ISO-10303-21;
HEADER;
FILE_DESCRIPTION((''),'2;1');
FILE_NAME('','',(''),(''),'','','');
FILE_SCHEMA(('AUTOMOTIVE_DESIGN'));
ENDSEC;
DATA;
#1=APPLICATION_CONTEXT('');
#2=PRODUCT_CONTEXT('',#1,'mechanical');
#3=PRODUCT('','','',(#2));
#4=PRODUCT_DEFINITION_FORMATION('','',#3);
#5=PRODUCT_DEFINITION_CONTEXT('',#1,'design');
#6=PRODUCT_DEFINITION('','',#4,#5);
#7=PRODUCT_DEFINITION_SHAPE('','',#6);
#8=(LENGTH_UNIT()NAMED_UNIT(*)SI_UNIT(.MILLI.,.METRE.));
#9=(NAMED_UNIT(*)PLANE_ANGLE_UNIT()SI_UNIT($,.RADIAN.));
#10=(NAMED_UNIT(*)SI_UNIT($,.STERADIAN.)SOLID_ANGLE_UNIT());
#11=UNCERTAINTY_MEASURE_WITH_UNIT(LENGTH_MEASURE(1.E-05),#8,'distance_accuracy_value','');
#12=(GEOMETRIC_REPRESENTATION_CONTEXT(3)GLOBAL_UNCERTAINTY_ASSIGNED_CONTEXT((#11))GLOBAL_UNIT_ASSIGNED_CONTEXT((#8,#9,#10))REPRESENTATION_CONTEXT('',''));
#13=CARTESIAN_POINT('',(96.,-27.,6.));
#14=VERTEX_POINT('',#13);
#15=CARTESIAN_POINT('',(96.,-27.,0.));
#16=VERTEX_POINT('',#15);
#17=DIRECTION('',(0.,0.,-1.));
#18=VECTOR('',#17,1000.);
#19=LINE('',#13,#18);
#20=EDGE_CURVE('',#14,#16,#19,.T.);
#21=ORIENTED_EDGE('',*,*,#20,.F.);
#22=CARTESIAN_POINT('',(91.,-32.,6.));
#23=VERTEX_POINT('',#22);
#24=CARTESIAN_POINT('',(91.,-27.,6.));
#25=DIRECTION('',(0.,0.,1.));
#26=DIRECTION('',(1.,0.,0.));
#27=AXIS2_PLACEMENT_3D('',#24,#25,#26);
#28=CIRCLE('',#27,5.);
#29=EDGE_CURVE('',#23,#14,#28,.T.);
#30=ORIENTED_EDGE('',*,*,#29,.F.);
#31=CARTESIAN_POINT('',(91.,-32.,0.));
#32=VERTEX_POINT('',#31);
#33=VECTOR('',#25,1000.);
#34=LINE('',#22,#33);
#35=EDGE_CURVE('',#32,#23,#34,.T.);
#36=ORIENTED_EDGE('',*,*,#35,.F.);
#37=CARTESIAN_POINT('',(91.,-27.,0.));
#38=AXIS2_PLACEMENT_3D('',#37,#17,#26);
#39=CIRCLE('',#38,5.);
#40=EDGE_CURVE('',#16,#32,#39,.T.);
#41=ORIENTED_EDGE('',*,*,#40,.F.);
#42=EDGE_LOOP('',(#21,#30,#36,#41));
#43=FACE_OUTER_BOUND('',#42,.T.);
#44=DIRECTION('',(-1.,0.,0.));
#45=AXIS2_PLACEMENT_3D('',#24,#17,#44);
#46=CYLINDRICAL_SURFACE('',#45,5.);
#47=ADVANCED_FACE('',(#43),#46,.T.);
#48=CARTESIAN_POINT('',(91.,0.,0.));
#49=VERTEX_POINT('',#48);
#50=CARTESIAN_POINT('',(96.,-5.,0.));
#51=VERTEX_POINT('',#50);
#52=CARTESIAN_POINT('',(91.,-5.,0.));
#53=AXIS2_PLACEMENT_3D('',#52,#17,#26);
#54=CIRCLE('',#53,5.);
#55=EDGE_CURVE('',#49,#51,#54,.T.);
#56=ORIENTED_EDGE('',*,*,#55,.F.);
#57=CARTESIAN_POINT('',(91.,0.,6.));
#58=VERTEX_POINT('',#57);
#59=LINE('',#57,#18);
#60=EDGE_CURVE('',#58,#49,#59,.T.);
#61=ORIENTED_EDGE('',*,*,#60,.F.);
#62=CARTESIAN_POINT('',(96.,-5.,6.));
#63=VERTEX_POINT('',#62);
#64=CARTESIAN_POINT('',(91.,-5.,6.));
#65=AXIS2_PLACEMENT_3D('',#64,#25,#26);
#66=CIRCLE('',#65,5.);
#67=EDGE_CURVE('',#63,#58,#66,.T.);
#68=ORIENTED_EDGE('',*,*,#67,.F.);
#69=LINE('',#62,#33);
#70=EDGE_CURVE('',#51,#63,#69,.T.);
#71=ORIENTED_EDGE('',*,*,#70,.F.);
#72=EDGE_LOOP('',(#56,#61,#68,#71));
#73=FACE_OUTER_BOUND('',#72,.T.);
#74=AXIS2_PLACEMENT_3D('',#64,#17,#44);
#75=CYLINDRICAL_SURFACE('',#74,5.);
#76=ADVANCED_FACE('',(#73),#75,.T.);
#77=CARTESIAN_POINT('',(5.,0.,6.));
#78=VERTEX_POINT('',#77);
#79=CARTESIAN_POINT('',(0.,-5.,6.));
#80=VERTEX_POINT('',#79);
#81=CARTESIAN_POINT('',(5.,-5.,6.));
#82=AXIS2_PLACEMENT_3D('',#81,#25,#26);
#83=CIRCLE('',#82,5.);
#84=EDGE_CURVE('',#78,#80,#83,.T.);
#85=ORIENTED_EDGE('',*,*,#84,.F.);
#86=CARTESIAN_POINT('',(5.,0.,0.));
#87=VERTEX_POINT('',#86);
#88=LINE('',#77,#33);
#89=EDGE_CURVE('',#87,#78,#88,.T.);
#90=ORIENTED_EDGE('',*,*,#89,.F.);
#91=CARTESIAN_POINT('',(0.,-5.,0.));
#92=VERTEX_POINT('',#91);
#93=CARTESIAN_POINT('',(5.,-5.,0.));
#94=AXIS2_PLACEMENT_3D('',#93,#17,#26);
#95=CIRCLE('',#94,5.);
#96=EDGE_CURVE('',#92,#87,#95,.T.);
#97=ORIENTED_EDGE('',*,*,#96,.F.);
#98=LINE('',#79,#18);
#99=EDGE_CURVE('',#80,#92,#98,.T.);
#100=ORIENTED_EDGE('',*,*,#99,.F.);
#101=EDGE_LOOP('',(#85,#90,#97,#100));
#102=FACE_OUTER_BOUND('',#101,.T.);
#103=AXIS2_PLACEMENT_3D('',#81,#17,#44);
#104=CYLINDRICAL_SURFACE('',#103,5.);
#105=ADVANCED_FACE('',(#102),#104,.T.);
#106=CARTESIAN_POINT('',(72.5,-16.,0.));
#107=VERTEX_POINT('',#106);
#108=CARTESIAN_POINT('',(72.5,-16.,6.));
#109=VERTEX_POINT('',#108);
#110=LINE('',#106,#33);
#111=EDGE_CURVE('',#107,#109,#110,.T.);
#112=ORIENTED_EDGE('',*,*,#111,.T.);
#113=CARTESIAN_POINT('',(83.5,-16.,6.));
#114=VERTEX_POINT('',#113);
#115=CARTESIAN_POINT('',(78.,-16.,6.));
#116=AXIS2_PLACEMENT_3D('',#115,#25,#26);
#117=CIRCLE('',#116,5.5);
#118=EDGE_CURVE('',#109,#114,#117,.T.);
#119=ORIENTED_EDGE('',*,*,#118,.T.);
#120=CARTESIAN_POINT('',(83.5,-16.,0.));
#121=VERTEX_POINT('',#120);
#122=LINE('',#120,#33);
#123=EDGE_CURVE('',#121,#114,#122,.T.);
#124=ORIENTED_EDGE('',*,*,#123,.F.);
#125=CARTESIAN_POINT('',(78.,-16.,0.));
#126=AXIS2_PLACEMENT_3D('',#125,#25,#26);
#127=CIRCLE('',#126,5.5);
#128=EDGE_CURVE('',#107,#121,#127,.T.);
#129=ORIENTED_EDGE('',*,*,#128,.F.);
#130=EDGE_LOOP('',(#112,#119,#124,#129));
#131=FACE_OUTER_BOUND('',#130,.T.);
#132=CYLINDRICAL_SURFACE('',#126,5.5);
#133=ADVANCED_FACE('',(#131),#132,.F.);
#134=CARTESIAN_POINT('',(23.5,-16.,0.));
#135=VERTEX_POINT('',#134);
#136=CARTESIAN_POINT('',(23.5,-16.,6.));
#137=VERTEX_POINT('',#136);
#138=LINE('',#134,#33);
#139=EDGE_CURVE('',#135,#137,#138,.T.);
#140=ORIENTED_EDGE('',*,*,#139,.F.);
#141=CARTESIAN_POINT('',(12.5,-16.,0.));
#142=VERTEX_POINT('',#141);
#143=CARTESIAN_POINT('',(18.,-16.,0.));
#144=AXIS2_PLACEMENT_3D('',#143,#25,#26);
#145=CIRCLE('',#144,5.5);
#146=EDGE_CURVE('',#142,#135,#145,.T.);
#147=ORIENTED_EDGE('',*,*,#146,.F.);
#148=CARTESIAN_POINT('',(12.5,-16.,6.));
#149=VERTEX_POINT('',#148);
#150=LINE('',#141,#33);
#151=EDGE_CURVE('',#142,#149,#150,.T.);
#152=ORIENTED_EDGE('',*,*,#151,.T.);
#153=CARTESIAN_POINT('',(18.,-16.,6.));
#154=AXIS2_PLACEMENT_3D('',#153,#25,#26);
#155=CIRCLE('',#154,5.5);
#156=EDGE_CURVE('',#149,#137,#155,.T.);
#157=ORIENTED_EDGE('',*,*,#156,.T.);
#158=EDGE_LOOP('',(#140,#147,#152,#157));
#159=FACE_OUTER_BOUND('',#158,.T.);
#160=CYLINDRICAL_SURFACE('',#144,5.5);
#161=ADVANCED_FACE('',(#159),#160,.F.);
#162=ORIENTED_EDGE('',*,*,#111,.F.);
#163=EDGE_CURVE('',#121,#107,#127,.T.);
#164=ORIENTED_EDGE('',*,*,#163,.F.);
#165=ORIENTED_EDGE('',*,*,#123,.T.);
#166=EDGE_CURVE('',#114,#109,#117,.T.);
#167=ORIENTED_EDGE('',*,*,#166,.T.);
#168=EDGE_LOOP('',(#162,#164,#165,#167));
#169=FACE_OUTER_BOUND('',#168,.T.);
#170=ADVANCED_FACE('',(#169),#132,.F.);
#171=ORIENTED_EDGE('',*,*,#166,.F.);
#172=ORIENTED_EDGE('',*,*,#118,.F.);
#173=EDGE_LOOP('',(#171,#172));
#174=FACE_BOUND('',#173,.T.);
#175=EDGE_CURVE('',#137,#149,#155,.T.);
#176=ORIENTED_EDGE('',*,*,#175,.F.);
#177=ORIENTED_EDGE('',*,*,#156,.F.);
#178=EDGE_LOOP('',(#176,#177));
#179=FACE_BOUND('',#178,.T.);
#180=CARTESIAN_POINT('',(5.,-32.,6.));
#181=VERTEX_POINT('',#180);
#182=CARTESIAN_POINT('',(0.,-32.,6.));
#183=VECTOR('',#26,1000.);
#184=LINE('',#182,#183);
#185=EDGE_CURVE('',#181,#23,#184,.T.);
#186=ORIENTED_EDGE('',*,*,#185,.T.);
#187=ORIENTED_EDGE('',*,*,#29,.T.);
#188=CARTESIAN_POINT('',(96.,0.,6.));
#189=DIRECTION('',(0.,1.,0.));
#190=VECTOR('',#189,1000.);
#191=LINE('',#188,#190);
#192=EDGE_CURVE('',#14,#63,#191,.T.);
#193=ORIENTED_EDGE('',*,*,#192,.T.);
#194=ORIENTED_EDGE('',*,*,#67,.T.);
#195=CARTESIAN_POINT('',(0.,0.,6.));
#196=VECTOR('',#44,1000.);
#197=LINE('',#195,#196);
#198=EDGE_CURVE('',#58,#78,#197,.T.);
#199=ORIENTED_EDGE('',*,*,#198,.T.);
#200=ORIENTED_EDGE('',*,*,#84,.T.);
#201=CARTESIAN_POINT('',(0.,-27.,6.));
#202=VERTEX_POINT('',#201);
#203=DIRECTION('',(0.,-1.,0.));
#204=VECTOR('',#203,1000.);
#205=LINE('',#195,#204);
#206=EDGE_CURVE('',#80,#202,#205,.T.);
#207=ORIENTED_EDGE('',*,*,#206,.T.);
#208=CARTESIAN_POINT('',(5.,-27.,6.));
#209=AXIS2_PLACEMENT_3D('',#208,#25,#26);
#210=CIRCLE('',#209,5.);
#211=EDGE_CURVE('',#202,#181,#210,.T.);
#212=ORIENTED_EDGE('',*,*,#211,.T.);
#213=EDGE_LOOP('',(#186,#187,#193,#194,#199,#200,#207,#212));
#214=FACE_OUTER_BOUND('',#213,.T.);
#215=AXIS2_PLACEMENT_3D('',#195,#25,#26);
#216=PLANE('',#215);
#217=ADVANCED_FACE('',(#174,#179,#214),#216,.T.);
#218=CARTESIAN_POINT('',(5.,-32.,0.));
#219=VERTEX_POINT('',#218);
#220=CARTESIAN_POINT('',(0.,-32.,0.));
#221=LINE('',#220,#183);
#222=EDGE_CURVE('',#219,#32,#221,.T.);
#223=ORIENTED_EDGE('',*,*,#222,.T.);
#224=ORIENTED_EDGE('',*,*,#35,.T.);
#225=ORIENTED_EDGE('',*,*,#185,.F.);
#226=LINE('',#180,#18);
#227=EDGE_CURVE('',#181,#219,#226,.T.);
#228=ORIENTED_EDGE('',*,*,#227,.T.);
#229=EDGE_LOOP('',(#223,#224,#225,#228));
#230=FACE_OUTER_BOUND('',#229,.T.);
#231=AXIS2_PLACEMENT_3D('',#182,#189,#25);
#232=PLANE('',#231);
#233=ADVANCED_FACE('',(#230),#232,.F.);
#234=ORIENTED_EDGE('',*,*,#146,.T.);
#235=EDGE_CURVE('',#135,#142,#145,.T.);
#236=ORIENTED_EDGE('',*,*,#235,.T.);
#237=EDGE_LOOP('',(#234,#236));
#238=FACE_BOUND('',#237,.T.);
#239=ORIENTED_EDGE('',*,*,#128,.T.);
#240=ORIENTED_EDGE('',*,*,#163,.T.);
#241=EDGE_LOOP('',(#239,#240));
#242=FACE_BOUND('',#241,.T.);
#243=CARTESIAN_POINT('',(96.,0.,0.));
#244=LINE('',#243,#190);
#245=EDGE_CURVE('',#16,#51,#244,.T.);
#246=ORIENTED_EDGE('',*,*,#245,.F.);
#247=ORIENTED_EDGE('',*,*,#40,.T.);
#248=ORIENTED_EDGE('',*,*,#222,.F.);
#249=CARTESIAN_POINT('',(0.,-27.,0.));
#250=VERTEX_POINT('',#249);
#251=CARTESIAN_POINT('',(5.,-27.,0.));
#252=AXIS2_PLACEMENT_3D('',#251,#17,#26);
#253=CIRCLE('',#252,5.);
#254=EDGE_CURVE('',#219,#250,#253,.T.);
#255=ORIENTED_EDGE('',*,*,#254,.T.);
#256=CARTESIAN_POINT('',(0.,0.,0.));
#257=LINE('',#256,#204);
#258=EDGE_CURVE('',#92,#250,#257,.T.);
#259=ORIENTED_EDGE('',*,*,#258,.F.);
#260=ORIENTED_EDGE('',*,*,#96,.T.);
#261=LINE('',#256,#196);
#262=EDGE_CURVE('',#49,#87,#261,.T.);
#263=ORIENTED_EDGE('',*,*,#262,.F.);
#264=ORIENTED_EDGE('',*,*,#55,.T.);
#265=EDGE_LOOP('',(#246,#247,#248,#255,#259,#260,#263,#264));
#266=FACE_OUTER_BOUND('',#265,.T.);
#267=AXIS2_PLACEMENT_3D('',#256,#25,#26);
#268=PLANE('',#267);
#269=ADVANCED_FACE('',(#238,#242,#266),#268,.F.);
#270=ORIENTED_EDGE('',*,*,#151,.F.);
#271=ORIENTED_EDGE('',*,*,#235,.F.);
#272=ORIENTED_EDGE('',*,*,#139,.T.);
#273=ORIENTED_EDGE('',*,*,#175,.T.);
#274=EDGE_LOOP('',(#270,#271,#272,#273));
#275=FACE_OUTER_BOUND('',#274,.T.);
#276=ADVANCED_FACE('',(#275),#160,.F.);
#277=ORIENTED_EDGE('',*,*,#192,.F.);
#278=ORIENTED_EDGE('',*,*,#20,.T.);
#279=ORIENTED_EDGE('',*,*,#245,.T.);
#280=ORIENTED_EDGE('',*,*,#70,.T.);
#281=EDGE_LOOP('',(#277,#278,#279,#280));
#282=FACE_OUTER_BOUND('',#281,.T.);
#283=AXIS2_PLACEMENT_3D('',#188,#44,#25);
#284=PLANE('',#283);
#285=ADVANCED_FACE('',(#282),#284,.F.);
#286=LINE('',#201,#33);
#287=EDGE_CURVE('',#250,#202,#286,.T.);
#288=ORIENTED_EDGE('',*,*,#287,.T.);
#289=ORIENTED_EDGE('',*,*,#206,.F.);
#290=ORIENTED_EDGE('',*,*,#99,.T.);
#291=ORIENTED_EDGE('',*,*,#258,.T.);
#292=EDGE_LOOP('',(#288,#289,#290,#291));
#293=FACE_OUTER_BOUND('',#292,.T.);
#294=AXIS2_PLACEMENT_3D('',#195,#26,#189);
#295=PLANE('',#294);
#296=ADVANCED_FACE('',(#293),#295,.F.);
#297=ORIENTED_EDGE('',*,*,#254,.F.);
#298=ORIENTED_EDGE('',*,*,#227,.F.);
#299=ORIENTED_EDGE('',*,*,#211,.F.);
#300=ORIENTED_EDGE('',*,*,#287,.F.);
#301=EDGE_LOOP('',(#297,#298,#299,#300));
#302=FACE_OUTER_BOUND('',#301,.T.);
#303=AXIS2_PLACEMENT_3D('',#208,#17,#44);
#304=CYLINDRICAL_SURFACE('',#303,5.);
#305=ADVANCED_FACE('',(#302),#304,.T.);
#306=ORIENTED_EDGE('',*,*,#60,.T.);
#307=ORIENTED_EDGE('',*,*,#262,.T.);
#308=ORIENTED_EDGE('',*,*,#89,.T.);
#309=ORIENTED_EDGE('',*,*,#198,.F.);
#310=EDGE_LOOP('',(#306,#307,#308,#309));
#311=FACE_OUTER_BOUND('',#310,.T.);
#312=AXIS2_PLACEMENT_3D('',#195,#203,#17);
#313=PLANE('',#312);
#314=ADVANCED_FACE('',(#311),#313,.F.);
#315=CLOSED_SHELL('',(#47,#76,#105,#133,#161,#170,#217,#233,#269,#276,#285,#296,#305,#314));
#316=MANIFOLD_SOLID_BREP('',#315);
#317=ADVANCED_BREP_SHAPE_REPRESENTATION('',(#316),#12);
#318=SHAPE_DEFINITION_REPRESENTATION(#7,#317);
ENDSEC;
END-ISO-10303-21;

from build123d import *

# Parameters (mm, degrees)
SKETCH1_W           = 96
SKETCH1_H           = 32
BOSS_EXTRUDE1_DEPTH = 6
FILLET1_R           = 5
SKETCH2_R           = 5.5
CUT_EXTRUDE1_DEPTH  = 6
LPATTERN1_COUNT     = 2
LPATTERN1_PITCH     = 60


with BuildPart() as part:
    # Sketch1 → Boss-Extrude1 (new body)
    with BuildSketch(Plane.XY):
        with Locations((48, -16)):
            Rectangle(SKETCH1_W, SKETCH1_H)
    extrude(amount=BOSS_EXTRUDE1_DEPTH)

    # Fillet1
    fillet1_edges = [part.edges().sort_by_distance(p)[0] for p in [
        (0, 0, 3),
        (96, 0, 3),
        (96, -32, 3),
        (0, -32, 3),
    ]]
    fillet(fillet1_edges, radius=FILLET1_R)

    # Sketch2 → Cut-Extrude1 (cut)
    with BuildSketch(Plane.XY.offset(6)):
        with Locations((18, -16)):
            Circle(SKETCH2_R)
    cut_extrude1 = extrude(amount=-CUT_EXTRUDE1_DEPTH, mode=Mode.SUBTRACT)

    # LPattern1: Cut-Extrude1 ×2
    with Locations(*[(i * LPATTERN1_PITCH, 0, 0) for i in range(1, LPATTERN1_COUNT)]):
        add(cut_extrude1, mode=Mode.SUBTRACT)


solid = part.part
